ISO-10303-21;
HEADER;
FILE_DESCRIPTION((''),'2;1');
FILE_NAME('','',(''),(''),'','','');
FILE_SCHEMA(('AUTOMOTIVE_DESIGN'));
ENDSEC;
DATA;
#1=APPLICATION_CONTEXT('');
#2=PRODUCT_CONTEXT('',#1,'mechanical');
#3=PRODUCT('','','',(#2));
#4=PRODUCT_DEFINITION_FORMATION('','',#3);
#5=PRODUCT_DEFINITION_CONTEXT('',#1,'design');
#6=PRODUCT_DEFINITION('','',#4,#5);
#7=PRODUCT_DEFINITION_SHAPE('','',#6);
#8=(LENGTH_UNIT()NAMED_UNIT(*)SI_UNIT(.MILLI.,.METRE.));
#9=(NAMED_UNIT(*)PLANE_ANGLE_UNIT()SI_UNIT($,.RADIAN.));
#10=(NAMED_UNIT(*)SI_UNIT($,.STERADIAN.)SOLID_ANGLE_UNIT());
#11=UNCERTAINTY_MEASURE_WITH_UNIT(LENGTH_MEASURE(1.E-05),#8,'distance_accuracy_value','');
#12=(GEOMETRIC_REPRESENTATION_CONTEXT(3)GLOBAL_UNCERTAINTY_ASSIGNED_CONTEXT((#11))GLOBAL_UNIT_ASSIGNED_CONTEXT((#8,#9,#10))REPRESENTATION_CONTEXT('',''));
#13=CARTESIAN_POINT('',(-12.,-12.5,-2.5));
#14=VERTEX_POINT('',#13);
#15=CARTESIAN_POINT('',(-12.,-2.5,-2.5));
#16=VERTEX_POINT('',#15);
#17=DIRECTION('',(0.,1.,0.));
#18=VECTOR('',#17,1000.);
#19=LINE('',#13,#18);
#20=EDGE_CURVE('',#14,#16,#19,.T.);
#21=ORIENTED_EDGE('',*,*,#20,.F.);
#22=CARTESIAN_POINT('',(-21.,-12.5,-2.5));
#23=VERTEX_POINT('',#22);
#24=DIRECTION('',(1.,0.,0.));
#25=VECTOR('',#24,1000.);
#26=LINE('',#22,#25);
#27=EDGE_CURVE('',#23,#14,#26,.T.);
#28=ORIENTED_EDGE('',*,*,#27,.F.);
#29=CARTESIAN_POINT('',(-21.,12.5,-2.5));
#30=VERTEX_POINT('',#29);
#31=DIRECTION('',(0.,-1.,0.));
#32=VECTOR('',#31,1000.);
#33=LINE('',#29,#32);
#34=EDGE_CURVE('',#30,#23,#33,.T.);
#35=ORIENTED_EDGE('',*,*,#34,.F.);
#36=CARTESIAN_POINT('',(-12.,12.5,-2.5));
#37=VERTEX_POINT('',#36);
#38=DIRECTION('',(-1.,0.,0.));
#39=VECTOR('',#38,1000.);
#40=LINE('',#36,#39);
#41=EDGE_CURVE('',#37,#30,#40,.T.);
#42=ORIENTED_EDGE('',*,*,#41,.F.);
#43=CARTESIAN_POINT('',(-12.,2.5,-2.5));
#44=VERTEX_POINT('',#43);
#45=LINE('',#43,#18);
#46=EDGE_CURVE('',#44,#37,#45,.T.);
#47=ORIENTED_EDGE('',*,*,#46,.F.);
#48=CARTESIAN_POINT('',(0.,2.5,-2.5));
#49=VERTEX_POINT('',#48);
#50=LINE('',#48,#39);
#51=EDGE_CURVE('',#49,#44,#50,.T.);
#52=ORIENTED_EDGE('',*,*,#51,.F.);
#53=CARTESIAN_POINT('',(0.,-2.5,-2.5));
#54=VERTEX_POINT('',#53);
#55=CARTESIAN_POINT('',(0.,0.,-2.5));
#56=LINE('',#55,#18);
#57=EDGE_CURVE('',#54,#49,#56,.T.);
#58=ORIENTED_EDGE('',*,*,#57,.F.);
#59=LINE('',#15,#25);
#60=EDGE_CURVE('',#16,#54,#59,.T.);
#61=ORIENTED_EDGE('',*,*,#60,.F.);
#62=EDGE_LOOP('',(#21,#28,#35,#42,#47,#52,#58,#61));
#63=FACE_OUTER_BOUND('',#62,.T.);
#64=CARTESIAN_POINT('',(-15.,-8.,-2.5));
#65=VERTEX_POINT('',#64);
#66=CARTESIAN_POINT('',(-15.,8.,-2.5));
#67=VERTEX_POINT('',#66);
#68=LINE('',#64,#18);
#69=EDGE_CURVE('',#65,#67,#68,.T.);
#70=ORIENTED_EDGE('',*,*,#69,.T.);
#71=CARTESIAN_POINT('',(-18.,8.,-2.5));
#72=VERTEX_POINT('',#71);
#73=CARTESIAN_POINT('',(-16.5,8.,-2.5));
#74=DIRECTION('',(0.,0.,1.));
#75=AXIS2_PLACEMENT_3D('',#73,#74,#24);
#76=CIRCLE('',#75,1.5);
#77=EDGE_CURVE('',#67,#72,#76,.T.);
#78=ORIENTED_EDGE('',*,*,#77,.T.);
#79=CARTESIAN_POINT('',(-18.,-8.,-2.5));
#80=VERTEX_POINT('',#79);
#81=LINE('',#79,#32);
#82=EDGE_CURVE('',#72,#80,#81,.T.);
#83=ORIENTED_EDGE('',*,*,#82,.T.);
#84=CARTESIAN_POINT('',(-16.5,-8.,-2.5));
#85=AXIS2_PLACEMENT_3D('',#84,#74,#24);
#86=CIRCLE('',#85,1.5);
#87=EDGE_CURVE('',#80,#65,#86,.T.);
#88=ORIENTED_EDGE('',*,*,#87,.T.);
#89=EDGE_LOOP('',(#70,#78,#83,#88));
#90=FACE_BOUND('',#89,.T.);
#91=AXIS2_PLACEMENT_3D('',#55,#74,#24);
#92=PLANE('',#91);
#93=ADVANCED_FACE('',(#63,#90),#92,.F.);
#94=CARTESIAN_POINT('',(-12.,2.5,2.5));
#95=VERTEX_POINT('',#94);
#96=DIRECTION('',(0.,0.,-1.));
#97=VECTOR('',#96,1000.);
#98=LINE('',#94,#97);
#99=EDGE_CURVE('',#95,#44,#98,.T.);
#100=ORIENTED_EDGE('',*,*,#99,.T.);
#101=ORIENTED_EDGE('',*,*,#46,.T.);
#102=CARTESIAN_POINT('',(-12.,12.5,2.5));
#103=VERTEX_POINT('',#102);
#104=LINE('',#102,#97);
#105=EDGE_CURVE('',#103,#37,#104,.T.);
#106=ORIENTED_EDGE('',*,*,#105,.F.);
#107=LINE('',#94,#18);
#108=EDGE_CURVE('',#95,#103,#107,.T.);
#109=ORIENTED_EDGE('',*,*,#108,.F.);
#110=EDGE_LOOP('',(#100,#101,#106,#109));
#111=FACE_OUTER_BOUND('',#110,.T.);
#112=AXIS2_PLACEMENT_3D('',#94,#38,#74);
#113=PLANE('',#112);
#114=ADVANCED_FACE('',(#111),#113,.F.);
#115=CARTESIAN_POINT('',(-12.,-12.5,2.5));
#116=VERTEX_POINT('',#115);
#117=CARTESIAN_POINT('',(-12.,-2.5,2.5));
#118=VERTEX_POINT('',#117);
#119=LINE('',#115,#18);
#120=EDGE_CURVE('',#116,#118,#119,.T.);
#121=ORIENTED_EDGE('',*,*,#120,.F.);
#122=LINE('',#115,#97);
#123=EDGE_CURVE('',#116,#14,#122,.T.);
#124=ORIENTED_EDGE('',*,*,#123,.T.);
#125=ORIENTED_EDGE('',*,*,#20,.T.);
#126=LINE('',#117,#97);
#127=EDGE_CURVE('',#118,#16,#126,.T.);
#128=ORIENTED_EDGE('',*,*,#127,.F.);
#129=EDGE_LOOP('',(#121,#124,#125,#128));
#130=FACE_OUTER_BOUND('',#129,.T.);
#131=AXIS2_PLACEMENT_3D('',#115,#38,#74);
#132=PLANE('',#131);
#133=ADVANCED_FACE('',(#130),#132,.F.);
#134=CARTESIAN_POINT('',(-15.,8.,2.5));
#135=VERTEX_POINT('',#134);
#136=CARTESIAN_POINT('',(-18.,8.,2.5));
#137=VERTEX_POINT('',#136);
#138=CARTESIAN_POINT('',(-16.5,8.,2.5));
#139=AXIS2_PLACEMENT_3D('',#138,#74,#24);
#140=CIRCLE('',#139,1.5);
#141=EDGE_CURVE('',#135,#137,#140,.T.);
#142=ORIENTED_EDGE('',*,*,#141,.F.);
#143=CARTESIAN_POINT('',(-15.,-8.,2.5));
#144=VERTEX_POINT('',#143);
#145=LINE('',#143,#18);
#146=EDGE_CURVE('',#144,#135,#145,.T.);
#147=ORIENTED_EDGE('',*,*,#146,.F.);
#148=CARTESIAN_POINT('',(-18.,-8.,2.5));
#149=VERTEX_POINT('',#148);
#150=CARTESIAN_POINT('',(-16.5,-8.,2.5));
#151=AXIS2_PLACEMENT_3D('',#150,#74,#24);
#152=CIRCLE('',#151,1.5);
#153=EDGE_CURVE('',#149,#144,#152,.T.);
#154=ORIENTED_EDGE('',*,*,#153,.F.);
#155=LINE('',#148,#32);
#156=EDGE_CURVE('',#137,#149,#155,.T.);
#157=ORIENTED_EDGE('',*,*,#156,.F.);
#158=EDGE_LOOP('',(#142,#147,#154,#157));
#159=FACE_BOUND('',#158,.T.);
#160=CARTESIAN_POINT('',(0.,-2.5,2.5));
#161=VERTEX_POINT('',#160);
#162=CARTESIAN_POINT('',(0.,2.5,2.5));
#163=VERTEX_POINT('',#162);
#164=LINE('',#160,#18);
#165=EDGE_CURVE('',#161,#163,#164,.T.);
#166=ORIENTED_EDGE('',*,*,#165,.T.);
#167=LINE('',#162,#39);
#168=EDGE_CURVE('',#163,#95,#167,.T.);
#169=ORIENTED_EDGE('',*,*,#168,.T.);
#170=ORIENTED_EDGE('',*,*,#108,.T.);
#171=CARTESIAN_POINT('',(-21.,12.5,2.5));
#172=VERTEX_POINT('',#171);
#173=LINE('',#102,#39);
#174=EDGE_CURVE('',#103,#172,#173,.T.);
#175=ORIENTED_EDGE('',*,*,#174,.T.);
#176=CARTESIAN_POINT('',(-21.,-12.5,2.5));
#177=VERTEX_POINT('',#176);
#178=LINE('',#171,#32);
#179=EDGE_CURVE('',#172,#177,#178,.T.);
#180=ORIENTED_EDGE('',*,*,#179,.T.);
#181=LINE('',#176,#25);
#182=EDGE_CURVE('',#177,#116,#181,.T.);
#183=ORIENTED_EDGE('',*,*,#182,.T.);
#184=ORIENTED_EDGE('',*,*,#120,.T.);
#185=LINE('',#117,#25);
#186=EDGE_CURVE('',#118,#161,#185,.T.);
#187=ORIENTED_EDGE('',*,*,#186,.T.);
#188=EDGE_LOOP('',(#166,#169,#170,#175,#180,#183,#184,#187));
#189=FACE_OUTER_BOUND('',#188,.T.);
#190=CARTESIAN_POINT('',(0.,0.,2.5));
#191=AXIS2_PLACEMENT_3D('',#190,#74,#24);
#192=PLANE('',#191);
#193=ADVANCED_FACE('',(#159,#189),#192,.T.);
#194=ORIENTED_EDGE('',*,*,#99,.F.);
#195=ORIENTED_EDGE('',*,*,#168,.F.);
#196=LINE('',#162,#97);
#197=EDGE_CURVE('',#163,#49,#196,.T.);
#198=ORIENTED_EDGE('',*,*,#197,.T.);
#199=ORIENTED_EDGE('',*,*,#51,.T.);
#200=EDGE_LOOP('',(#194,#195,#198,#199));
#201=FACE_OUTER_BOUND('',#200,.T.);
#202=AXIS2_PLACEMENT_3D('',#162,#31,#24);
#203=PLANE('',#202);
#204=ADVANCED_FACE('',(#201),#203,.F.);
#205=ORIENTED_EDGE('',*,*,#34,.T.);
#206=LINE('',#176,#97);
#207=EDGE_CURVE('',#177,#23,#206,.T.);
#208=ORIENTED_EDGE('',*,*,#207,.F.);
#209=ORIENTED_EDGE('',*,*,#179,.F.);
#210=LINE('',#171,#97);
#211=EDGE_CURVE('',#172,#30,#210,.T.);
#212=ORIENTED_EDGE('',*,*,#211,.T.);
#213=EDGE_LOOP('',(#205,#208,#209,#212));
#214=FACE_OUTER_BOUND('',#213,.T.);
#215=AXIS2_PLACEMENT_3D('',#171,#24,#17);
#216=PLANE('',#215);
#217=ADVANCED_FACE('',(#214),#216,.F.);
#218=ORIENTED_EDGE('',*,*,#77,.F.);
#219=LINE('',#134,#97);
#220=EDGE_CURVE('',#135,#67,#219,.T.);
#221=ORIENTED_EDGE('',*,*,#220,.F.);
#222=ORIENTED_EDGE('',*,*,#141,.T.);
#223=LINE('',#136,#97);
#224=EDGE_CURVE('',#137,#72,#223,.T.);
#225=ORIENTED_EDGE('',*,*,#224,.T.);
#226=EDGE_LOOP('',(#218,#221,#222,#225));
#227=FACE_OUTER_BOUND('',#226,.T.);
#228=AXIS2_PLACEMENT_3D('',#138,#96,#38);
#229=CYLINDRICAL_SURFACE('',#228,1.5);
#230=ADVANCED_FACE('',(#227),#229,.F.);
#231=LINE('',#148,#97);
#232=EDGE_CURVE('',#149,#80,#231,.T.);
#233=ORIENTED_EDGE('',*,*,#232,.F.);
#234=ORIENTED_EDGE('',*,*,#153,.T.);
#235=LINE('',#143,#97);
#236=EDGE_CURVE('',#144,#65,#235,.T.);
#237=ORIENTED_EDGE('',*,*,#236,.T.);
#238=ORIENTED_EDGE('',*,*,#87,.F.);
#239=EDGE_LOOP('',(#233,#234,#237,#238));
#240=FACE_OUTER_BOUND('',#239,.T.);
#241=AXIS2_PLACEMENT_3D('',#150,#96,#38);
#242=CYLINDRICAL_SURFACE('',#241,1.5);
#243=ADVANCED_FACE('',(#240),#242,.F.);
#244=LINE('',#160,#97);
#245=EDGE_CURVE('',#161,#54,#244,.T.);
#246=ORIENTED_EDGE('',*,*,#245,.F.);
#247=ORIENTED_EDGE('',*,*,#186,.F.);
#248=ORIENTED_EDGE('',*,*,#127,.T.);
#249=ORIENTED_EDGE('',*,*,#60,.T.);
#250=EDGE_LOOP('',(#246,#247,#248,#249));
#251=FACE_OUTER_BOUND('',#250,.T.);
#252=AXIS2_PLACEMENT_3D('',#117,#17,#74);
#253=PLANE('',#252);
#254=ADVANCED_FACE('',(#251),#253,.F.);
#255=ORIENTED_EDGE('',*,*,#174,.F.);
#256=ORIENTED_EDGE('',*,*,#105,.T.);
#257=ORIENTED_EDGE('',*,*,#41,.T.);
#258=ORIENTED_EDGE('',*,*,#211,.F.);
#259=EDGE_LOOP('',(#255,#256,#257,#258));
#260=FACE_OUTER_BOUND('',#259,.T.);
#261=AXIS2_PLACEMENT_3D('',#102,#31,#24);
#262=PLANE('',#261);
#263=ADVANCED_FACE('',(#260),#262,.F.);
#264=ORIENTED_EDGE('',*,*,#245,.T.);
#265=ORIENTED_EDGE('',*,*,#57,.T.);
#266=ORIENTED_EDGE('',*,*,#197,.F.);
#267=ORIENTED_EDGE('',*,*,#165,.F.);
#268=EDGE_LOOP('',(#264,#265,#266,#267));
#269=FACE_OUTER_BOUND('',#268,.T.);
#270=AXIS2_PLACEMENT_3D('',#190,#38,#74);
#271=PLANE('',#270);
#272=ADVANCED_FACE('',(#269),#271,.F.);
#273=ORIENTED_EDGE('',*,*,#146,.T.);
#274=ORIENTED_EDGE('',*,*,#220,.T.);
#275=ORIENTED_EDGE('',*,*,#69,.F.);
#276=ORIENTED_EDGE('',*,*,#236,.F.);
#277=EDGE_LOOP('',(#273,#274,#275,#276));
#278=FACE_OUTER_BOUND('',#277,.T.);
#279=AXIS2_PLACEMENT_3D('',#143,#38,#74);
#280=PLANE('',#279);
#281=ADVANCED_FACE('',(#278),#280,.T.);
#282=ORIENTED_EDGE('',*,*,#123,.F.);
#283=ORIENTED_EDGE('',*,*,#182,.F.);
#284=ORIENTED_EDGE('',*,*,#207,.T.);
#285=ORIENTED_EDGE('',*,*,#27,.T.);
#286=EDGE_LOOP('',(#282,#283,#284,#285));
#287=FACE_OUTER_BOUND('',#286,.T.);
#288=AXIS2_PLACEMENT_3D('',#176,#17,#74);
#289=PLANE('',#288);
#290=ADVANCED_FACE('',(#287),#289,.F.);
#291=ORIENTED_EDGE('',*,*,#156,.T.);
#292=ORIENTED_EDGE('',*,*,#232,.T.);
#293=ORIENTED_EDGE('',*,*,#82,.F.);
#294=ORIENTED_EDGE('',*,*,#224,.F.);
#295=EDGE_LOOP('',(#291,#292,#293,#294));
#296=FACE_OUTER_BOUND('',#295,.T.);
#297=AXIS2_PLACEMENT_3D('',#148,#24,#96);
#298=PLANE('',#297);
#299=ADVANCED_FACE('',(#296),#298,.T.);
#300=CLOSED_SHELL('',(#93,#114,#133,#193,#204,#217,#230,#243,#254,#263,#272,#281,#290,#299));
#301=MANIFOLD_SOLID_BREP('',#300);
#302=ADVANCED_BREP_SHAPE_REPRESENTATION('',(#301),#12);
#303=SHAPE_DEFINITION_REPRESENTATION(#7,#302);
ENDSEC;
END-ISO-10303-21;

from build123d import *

# Parameters (mm, degrees)
EXTRUDE_1_DEPTH = 2.5


with BuildPart() as part:
    # 草图1 → 凸台-拉伸1 (new, symmetric)
    with BuildSketch(Plane.XY):
        Polygon((0, 0), (0, 2.5), (-12, 2.5), (-12, 12.5), (-21, 12.5), (-21, -12.5), (-12, -12.5), (-12, -2.5), (0, -2.5), align=None)
        with BuildLine():
            Line((-18, -8), (-18, 8))
            ThreePointArc((-18, 8), (-16.5, 9.5), (-15, 8))
            Line((-15, 8), (-15, -8))
            ThreePointArc((-15, -8), (-16.5, -9.5), (-18, -8))
        make_face(mode=Mode.SUBTRACT)
    extrude(amount=EXTRUDE_1_DEPTH, both=True)


solid = part.part
